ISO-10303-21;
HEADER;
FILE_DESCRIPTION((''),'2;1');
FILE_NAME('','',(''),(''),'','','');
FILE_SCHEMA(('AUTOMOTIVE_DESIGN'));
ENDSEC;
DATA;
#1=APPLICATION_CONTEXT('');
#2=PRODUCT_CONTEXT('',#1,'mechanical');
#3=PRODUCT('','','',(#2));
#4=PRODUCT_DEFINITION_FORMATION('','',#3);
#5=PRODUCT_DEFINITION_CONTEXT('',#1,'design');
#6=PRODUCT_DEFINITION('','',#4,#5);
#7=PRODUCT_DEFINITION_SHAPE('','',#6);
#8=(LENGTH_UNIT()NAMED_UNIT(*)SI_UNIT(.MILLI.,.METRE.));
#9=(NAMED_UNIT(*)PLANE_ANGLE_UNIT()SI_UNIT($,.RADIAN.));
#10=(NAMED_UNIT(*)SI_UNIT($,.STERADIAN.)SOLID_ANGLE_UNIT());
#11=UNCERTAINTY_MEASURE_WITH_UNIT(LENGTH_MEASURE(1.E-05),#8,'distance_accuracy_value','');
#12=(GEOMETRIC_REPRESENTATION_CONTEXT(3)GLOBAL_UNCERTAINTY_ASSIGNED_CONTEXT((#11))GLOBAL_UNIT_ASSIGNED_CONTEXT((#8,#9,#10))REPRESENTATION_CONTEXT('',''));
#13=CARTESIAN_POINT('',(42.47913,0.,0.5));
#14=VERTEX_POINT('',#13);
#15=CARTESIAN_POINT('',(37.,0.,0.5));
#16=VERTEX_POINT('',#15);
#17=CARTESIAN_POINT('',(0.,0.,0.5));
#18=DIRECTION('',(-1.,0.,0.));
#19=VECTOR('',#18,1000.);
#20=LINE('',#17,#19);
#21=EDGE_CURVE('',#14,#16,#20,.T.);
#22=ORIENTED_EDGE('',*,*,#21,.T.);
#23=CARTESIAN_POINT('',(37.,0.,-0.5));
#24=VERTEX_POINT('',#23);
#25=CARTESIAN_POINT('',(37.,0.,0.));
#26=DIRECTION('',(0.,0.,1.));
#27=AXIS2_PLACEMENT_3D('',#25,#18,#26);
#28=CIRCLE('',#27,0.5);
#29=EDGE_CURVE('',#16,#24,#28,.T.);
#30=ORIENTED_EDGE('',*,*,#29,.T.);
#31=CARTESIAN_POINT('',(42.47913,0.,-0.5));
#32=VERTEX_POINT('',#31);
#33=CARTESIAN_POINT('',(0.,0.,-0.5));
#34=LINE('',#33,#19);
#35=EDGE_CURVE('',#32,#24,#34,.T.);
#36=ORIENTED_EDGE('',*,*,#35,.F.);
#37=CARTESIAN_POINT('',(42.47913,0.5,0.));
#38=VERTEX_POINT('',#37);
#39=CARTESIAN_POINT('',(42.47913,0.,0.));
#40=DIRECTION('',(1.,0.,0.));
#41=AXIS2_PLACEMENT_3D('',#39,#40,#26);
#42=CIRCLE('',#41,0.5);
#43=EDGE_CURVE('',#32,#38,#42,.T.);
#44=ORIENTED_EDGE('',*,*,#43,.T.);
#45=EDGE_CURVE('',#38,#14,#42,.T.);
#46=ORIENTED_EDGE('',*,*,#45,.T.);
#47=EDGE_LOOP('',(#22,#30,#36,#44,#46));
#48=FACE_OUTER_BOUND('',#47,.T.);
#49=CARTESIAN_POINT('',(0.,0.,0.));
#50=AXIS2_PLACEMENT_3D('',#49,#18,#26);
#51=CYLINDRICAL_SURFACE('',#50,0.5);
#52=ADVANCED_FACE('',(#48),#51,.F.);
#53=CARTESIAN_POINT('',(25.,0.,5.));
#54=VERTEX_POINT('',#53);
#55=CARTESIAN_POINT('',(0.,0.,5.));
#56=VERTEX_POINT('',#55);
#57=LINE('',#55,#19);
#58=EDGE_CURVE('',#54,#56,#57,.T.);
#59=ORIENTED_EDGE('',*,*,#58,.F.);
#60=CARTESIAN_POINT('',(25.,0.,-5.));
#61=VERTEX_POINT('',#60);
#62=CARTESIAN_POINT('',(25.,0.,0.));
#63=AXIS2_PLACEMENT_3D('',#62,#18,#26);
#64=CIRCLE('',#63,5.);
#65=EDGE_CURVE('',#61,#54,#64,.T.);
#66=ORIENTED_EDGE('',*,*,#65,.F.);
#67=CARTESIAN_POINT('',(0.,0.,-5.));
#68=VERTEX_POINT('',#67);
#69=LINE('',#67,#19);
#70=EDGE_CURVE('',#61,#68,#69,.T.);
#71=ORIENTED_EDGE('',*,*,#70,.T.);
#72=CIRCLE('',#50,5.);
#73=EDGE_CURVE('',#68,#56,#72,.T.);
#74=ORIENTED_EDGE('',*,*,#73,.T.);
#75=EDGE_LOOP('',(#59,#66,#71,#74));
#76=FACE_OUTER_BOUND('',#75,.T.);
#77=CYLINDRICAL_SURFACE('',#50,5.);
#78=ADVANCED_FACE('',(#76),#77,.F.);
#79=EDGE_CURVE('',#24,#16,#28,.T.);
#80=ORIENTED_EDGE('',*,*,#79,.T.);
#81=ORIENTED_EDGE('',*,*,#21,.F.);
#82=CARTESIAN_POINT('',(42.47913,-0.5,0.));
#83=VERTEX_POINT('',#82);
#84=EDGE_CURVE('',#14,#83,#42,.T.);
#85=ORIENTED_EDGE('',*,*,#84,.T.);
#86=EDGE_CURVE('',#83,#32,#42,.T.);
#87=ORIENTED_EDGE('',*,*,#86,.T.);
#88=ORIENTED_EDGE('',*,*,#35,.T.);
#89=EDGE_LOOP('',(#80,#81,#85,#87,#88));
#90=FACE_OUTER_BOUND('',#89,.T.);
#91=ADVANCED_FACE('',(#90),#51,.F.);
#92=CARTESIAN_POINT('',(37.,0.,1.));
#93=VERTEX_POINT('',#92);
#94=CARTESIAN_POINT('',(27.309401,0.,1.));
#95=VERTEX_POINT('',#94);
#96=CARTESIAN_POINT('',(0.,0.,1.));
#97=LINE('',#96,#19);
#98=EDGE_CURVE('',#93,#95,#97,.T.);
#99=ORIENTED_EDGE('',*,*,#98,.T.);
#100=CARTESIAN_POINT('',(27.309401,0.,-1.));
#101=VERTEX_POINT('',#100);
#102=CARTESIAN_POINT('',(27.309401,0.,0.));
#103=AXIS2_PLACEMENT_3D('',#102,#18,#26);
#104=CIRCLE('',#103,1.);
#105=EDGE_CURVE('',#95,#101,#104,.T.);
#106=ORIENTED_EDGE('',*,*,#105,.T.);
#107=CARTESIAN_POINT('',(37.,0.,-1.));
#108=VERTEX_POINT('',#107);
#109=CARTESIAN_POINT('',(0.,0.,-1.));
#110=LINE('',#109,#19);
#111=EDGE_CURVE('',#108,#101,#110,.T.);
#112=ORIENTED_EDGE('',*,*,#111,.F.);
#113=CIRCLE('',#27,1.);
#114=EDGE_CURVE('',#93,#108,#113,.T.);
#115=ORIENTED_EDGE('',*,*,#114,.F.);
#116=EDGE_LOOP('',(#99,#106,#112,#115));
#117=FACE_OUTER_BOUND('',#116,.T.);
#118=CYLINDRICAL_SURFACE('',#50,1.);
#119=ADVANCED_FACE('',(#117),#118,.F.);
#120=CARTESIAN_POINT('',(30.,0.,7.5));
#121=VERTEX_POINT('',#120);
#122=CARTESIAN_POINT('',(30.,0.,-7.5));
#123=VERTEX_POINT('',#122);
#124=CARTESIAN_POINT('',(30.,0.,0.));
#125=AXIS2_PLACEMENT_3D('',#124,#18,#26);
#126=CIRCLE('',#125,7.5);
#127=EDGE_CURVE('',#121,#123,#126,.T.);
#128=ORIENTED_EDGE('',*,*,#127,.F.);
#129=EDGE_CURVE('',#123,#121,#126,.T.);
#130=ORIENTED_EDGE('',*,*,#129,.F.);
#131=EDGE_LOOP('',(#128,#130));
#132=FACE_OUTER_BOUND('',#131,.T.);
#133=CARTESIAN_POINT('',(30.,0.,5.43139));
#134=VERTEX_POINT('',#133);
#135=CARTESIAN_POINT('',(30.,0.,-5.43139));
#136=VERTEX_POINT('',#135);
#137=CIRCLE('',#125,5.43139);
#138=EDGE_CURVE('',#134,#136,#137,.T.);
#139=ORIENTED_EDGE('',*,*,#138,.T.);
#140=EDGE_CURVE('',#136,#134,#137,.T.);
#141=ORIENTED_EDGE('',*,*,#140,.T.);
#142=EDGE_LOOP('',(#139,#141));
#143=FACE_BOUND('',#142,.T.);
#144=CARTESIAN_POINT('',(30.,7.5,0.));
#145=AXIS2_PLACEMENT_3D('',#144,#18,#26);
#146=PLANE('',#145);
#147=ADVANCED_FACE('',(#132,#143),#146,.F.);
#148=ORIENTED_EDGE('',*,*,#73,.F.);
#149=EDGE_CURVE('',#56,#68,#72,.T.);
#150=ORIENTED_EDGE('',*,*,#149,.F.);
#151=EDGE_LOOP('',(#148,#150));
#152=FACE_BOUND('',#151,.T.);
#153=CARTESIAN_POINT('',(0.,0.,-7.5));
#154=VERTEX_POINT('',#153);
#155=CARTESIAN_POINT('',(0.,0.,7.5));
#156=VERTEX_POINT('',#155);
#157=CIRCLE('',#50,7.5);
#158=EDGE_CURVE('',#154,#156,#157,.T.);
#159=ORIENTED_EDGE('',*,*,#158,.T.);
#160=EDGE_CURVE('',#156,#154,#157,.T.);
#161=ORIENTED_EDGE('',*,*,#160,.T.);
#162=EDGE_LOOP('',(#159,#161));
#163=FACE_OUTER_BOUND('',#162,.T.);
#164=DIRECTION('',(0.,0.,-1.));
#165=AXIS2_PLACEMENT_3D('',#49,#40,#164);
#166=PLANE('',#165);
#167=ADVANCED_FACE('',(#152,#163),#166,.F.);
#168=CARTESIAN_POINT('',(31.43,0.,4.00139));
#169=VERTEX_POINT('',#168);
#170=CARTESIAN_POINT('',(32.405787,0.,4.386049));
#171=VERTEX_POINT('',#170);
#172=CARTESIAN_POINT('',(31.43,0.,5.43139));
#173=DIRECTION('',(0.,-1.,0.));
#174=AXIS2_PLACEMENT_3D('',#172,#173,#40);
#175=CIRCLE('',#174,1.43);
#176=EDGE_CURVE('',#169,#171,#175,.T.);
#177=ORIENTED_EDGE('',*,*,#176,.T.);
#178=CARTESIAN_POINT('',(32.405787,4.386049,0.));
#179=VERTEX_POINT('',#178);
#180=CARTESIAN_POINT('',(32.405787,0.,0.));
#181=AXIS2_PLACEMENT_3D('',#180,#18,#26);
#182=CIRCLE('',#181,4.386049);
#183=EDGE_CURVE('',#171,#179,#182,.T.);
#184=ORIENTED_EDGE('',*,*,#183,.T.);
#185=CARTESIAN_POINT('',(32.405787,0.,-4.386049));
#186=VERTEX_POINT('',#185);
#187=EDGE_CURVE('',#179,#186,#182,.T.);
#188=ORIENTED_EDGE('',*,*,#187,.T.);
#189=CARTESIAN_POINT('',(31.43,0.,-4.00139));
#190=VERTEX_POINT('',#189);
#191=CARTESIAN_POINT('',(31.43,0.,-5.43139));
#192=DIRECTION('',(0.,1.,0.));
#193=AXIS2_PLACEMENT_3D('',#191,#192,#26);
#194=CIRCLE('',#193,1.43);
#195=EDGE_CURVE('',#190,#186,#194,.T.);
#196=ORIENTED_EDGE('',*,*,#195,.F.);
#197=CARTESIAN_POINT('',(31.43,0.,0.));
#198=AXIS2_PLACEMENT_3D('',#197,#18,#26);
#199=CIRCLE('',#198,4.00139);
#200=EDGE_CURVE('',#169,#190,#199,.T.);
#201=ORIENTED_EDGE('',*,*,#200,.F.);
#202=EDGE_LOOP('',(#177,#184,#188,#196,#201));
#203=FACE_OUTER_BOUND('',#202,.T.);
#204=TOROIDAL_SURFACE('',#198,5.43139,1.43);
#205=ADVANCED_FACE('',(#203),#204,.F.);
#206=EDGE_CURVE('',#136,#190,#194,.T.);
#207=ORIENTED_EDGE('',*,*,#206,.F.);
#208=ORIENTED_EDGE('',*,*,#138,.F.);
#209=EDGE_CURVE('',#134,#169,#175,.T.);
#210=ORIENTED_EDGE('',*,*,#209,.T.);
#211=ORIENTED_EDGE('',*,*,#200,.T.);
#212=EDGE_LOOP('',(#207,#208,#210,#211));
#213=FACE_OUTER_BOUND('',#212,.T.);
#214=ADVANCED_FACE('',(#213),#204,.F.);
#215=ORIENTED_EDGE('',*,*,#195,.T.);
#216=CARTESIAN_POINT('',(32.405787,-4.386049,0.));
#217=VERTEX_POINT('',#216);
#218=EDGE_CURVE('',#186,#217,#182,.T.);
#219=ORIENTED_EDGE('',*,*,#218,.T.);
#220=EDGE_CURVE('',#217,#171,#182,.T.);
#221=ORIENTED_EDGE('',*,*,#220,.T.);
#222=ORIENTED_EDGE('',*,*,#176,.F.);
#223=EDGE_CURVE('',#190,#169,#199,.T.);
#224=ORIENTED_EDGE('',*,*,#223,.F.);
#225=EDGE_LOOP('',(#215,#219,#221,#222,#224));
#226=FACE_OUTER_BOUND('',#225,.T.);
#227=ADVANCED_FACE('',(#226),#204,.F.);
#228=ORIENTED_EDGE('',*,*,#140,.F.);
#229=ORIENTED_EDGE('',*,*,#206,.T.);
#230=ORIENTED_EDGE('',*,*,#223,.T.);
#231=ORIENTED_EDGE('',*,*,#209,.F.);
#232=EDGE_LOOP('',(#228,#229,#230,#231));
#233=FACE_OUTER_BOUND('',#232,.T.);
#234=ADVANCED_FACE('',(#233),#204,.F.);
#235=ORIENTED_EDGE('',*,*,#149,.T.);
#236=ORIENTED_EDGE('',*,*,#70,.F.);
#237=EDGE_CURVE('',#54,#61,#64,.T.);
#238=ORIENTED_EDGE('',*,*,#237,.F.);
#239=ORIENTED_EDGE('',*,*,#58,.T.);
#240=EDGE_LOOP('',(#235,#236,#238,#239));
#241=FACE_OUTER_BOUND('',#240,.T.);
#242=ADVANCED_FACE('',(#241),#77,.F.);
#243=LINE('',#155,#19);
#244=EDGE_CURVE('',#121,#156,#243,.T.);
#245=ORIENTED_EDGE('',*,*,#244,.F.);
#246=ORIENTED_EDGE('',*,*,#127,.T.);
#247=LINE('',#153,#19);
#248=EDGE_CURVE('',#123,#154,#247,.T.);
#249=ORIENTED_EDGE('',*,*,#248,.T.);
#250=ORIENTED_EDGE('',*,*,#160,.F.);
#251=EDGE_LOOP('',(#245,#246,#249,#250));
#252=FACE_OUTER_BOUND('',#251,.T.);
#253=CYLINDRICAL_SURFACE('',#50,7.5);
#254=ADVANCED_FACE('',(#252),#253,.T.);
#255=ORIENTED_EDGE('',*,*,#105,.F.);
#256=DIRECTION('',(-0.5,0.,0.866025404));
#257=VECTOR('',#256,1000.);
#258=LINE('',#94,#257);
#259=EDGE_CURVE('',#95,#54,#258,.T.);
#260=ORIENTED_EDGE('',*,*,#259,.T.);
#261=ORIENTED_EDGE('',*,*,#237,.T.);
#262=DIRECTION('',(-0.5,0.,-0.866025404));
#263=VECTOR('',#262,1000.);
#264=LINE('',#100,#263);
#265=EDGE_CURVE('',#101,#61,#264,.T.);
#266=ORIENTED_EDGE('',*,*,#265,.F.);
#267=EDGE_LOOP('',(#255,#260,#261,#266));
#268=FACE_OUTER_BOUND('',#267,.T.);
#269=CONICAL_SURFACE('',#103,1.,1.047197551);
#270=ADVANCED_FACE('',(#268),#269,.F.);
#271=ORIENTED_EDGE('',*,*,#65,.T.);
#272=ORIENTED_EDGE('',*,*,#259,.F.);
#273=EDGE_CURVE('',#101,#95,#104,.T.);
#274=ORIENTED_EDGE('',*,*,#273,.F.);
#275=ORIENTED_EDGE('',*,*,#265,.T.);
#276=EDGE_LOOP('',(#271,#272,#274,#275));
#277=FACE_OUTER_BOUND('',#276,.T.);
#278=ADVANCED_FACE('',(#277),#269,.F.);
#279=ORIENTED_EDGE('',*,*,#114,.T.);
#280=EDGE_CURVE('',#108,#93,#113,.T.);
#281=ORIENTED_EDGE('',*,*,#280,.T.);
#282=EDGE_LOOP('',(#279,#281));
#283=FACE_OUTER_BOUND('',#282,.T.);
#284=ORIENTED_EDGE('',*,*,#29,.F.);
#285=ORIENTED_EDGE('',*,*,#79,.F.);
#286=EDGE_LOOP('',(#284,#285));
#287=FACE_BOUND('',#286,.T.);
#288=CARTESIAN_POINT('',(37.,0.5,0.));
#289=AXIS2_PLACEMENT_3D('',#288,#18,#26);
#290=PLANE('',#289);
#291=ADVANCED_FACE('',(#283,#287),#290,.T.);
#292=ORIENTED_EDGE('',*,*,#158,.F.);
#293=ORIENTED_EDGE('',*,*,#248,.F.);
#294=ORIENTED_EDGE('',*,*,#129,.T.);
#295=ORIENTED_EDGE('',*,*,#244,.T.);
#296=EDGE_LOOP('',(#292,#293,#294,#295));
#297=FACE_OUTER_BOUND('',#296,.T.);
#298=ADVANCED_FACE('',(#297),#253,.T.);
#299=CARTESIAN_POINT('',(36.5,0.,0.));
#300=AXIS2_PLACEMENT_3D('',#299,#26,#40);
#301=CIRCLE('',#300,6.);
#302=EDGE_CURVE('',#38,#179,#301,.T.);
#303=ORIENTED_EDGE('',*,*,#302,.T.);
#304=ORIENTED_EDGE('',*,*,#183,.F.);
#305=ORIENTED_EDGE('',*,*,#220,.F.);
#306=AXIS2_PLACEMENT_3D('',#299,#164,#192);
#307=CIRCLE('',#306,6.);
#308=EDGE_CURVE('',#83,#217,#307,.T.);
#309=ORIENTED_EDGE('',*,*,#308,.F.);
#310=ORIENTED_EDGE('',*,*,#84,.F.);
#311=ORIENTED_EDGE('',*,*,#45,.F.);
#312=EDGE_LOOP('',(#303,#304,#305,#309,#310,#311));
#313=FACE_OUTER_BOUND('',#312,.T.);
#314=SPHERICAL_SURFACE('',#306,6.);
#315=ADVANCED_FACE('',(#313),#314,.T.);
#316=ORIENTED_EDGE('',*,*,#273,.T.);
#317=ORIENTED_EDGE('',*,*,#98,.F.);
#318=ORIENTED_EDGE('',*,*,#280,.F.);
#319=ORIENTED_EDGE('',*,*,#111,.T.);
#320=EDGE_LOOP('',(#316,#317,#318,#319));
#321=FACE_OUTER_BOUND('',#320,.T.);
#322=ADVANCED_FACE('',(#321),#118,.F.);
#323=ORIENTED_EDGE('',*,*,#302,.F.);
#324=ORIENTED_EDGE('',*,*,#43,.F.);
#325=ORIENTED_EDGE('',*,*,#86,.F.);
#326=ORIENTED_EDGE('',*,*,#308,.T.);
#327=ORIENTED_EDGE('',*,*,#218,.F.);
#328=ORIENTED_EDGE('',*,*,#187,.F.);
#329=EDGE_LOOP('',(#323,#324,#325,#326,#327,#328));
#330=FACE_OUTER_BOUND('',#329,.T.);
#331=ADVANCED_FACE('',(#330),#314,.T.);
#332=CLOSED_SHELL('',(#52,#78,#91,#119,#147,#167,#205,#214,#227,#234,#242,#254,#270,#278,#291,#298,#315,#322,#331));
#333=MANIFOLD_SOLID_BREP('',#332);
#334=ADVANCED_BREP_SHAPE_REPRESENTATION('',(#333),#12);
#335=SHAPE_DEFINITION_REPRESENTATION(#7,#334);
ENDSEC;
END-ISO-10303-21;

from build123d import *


with BuildPart() as part:
    # Sketch1 → Revolve1 (revolve)
    with BuildSketch(Plane.XY, mode=Mode.PRIVATE) as revolve1_sk:
        with BuildLine():
            Line((0, 0), (0, 7.5))
            Line((0, 7.5), (30, 7.5))
            Line((30, 7.5), (30, 5.431390246))
            ThreePointArc((30, 5.431390246), (30.860121025, 4.119849947), (32.405787349, 4.386048651))
            ThreePointArc((32.405787349, 4.386048651), (38.891100593, 5.502966287), (42.5, 0))
            Line((42.5, 0), (0, 0))
        make_face()
    revolve(revolve1_sk.sketch.rotate(Axis((0, 0, 0), (1, 0, 0)), 90), axis=Axis((0, 0, 0), (1, 0, 0)))

    # Sketch2 → Cut-Revolve1 (revolve, cut)
    with BuildSketch(Plane.XY, mode=Mode.PRIVATE) as cut_revolve1_sk:
        Polygon((0, 0), (25, 0), (27.309401077, 0), (37, 0), (47.95408822, 0), (47.95408822, 0.5), (37, 0.5), (37, 1), (27.309401077, 1), (25, 5), (0, 5), align=None)
    revolve(cut_revolve1_sk.sketch.rotate(Axis((0, 0, 0), (1, 0, 0)), 90), axis=Axis((0, 0, 0), (1, 0, 0)), mode=Mode.SUBTRACT)


solid = part.part
